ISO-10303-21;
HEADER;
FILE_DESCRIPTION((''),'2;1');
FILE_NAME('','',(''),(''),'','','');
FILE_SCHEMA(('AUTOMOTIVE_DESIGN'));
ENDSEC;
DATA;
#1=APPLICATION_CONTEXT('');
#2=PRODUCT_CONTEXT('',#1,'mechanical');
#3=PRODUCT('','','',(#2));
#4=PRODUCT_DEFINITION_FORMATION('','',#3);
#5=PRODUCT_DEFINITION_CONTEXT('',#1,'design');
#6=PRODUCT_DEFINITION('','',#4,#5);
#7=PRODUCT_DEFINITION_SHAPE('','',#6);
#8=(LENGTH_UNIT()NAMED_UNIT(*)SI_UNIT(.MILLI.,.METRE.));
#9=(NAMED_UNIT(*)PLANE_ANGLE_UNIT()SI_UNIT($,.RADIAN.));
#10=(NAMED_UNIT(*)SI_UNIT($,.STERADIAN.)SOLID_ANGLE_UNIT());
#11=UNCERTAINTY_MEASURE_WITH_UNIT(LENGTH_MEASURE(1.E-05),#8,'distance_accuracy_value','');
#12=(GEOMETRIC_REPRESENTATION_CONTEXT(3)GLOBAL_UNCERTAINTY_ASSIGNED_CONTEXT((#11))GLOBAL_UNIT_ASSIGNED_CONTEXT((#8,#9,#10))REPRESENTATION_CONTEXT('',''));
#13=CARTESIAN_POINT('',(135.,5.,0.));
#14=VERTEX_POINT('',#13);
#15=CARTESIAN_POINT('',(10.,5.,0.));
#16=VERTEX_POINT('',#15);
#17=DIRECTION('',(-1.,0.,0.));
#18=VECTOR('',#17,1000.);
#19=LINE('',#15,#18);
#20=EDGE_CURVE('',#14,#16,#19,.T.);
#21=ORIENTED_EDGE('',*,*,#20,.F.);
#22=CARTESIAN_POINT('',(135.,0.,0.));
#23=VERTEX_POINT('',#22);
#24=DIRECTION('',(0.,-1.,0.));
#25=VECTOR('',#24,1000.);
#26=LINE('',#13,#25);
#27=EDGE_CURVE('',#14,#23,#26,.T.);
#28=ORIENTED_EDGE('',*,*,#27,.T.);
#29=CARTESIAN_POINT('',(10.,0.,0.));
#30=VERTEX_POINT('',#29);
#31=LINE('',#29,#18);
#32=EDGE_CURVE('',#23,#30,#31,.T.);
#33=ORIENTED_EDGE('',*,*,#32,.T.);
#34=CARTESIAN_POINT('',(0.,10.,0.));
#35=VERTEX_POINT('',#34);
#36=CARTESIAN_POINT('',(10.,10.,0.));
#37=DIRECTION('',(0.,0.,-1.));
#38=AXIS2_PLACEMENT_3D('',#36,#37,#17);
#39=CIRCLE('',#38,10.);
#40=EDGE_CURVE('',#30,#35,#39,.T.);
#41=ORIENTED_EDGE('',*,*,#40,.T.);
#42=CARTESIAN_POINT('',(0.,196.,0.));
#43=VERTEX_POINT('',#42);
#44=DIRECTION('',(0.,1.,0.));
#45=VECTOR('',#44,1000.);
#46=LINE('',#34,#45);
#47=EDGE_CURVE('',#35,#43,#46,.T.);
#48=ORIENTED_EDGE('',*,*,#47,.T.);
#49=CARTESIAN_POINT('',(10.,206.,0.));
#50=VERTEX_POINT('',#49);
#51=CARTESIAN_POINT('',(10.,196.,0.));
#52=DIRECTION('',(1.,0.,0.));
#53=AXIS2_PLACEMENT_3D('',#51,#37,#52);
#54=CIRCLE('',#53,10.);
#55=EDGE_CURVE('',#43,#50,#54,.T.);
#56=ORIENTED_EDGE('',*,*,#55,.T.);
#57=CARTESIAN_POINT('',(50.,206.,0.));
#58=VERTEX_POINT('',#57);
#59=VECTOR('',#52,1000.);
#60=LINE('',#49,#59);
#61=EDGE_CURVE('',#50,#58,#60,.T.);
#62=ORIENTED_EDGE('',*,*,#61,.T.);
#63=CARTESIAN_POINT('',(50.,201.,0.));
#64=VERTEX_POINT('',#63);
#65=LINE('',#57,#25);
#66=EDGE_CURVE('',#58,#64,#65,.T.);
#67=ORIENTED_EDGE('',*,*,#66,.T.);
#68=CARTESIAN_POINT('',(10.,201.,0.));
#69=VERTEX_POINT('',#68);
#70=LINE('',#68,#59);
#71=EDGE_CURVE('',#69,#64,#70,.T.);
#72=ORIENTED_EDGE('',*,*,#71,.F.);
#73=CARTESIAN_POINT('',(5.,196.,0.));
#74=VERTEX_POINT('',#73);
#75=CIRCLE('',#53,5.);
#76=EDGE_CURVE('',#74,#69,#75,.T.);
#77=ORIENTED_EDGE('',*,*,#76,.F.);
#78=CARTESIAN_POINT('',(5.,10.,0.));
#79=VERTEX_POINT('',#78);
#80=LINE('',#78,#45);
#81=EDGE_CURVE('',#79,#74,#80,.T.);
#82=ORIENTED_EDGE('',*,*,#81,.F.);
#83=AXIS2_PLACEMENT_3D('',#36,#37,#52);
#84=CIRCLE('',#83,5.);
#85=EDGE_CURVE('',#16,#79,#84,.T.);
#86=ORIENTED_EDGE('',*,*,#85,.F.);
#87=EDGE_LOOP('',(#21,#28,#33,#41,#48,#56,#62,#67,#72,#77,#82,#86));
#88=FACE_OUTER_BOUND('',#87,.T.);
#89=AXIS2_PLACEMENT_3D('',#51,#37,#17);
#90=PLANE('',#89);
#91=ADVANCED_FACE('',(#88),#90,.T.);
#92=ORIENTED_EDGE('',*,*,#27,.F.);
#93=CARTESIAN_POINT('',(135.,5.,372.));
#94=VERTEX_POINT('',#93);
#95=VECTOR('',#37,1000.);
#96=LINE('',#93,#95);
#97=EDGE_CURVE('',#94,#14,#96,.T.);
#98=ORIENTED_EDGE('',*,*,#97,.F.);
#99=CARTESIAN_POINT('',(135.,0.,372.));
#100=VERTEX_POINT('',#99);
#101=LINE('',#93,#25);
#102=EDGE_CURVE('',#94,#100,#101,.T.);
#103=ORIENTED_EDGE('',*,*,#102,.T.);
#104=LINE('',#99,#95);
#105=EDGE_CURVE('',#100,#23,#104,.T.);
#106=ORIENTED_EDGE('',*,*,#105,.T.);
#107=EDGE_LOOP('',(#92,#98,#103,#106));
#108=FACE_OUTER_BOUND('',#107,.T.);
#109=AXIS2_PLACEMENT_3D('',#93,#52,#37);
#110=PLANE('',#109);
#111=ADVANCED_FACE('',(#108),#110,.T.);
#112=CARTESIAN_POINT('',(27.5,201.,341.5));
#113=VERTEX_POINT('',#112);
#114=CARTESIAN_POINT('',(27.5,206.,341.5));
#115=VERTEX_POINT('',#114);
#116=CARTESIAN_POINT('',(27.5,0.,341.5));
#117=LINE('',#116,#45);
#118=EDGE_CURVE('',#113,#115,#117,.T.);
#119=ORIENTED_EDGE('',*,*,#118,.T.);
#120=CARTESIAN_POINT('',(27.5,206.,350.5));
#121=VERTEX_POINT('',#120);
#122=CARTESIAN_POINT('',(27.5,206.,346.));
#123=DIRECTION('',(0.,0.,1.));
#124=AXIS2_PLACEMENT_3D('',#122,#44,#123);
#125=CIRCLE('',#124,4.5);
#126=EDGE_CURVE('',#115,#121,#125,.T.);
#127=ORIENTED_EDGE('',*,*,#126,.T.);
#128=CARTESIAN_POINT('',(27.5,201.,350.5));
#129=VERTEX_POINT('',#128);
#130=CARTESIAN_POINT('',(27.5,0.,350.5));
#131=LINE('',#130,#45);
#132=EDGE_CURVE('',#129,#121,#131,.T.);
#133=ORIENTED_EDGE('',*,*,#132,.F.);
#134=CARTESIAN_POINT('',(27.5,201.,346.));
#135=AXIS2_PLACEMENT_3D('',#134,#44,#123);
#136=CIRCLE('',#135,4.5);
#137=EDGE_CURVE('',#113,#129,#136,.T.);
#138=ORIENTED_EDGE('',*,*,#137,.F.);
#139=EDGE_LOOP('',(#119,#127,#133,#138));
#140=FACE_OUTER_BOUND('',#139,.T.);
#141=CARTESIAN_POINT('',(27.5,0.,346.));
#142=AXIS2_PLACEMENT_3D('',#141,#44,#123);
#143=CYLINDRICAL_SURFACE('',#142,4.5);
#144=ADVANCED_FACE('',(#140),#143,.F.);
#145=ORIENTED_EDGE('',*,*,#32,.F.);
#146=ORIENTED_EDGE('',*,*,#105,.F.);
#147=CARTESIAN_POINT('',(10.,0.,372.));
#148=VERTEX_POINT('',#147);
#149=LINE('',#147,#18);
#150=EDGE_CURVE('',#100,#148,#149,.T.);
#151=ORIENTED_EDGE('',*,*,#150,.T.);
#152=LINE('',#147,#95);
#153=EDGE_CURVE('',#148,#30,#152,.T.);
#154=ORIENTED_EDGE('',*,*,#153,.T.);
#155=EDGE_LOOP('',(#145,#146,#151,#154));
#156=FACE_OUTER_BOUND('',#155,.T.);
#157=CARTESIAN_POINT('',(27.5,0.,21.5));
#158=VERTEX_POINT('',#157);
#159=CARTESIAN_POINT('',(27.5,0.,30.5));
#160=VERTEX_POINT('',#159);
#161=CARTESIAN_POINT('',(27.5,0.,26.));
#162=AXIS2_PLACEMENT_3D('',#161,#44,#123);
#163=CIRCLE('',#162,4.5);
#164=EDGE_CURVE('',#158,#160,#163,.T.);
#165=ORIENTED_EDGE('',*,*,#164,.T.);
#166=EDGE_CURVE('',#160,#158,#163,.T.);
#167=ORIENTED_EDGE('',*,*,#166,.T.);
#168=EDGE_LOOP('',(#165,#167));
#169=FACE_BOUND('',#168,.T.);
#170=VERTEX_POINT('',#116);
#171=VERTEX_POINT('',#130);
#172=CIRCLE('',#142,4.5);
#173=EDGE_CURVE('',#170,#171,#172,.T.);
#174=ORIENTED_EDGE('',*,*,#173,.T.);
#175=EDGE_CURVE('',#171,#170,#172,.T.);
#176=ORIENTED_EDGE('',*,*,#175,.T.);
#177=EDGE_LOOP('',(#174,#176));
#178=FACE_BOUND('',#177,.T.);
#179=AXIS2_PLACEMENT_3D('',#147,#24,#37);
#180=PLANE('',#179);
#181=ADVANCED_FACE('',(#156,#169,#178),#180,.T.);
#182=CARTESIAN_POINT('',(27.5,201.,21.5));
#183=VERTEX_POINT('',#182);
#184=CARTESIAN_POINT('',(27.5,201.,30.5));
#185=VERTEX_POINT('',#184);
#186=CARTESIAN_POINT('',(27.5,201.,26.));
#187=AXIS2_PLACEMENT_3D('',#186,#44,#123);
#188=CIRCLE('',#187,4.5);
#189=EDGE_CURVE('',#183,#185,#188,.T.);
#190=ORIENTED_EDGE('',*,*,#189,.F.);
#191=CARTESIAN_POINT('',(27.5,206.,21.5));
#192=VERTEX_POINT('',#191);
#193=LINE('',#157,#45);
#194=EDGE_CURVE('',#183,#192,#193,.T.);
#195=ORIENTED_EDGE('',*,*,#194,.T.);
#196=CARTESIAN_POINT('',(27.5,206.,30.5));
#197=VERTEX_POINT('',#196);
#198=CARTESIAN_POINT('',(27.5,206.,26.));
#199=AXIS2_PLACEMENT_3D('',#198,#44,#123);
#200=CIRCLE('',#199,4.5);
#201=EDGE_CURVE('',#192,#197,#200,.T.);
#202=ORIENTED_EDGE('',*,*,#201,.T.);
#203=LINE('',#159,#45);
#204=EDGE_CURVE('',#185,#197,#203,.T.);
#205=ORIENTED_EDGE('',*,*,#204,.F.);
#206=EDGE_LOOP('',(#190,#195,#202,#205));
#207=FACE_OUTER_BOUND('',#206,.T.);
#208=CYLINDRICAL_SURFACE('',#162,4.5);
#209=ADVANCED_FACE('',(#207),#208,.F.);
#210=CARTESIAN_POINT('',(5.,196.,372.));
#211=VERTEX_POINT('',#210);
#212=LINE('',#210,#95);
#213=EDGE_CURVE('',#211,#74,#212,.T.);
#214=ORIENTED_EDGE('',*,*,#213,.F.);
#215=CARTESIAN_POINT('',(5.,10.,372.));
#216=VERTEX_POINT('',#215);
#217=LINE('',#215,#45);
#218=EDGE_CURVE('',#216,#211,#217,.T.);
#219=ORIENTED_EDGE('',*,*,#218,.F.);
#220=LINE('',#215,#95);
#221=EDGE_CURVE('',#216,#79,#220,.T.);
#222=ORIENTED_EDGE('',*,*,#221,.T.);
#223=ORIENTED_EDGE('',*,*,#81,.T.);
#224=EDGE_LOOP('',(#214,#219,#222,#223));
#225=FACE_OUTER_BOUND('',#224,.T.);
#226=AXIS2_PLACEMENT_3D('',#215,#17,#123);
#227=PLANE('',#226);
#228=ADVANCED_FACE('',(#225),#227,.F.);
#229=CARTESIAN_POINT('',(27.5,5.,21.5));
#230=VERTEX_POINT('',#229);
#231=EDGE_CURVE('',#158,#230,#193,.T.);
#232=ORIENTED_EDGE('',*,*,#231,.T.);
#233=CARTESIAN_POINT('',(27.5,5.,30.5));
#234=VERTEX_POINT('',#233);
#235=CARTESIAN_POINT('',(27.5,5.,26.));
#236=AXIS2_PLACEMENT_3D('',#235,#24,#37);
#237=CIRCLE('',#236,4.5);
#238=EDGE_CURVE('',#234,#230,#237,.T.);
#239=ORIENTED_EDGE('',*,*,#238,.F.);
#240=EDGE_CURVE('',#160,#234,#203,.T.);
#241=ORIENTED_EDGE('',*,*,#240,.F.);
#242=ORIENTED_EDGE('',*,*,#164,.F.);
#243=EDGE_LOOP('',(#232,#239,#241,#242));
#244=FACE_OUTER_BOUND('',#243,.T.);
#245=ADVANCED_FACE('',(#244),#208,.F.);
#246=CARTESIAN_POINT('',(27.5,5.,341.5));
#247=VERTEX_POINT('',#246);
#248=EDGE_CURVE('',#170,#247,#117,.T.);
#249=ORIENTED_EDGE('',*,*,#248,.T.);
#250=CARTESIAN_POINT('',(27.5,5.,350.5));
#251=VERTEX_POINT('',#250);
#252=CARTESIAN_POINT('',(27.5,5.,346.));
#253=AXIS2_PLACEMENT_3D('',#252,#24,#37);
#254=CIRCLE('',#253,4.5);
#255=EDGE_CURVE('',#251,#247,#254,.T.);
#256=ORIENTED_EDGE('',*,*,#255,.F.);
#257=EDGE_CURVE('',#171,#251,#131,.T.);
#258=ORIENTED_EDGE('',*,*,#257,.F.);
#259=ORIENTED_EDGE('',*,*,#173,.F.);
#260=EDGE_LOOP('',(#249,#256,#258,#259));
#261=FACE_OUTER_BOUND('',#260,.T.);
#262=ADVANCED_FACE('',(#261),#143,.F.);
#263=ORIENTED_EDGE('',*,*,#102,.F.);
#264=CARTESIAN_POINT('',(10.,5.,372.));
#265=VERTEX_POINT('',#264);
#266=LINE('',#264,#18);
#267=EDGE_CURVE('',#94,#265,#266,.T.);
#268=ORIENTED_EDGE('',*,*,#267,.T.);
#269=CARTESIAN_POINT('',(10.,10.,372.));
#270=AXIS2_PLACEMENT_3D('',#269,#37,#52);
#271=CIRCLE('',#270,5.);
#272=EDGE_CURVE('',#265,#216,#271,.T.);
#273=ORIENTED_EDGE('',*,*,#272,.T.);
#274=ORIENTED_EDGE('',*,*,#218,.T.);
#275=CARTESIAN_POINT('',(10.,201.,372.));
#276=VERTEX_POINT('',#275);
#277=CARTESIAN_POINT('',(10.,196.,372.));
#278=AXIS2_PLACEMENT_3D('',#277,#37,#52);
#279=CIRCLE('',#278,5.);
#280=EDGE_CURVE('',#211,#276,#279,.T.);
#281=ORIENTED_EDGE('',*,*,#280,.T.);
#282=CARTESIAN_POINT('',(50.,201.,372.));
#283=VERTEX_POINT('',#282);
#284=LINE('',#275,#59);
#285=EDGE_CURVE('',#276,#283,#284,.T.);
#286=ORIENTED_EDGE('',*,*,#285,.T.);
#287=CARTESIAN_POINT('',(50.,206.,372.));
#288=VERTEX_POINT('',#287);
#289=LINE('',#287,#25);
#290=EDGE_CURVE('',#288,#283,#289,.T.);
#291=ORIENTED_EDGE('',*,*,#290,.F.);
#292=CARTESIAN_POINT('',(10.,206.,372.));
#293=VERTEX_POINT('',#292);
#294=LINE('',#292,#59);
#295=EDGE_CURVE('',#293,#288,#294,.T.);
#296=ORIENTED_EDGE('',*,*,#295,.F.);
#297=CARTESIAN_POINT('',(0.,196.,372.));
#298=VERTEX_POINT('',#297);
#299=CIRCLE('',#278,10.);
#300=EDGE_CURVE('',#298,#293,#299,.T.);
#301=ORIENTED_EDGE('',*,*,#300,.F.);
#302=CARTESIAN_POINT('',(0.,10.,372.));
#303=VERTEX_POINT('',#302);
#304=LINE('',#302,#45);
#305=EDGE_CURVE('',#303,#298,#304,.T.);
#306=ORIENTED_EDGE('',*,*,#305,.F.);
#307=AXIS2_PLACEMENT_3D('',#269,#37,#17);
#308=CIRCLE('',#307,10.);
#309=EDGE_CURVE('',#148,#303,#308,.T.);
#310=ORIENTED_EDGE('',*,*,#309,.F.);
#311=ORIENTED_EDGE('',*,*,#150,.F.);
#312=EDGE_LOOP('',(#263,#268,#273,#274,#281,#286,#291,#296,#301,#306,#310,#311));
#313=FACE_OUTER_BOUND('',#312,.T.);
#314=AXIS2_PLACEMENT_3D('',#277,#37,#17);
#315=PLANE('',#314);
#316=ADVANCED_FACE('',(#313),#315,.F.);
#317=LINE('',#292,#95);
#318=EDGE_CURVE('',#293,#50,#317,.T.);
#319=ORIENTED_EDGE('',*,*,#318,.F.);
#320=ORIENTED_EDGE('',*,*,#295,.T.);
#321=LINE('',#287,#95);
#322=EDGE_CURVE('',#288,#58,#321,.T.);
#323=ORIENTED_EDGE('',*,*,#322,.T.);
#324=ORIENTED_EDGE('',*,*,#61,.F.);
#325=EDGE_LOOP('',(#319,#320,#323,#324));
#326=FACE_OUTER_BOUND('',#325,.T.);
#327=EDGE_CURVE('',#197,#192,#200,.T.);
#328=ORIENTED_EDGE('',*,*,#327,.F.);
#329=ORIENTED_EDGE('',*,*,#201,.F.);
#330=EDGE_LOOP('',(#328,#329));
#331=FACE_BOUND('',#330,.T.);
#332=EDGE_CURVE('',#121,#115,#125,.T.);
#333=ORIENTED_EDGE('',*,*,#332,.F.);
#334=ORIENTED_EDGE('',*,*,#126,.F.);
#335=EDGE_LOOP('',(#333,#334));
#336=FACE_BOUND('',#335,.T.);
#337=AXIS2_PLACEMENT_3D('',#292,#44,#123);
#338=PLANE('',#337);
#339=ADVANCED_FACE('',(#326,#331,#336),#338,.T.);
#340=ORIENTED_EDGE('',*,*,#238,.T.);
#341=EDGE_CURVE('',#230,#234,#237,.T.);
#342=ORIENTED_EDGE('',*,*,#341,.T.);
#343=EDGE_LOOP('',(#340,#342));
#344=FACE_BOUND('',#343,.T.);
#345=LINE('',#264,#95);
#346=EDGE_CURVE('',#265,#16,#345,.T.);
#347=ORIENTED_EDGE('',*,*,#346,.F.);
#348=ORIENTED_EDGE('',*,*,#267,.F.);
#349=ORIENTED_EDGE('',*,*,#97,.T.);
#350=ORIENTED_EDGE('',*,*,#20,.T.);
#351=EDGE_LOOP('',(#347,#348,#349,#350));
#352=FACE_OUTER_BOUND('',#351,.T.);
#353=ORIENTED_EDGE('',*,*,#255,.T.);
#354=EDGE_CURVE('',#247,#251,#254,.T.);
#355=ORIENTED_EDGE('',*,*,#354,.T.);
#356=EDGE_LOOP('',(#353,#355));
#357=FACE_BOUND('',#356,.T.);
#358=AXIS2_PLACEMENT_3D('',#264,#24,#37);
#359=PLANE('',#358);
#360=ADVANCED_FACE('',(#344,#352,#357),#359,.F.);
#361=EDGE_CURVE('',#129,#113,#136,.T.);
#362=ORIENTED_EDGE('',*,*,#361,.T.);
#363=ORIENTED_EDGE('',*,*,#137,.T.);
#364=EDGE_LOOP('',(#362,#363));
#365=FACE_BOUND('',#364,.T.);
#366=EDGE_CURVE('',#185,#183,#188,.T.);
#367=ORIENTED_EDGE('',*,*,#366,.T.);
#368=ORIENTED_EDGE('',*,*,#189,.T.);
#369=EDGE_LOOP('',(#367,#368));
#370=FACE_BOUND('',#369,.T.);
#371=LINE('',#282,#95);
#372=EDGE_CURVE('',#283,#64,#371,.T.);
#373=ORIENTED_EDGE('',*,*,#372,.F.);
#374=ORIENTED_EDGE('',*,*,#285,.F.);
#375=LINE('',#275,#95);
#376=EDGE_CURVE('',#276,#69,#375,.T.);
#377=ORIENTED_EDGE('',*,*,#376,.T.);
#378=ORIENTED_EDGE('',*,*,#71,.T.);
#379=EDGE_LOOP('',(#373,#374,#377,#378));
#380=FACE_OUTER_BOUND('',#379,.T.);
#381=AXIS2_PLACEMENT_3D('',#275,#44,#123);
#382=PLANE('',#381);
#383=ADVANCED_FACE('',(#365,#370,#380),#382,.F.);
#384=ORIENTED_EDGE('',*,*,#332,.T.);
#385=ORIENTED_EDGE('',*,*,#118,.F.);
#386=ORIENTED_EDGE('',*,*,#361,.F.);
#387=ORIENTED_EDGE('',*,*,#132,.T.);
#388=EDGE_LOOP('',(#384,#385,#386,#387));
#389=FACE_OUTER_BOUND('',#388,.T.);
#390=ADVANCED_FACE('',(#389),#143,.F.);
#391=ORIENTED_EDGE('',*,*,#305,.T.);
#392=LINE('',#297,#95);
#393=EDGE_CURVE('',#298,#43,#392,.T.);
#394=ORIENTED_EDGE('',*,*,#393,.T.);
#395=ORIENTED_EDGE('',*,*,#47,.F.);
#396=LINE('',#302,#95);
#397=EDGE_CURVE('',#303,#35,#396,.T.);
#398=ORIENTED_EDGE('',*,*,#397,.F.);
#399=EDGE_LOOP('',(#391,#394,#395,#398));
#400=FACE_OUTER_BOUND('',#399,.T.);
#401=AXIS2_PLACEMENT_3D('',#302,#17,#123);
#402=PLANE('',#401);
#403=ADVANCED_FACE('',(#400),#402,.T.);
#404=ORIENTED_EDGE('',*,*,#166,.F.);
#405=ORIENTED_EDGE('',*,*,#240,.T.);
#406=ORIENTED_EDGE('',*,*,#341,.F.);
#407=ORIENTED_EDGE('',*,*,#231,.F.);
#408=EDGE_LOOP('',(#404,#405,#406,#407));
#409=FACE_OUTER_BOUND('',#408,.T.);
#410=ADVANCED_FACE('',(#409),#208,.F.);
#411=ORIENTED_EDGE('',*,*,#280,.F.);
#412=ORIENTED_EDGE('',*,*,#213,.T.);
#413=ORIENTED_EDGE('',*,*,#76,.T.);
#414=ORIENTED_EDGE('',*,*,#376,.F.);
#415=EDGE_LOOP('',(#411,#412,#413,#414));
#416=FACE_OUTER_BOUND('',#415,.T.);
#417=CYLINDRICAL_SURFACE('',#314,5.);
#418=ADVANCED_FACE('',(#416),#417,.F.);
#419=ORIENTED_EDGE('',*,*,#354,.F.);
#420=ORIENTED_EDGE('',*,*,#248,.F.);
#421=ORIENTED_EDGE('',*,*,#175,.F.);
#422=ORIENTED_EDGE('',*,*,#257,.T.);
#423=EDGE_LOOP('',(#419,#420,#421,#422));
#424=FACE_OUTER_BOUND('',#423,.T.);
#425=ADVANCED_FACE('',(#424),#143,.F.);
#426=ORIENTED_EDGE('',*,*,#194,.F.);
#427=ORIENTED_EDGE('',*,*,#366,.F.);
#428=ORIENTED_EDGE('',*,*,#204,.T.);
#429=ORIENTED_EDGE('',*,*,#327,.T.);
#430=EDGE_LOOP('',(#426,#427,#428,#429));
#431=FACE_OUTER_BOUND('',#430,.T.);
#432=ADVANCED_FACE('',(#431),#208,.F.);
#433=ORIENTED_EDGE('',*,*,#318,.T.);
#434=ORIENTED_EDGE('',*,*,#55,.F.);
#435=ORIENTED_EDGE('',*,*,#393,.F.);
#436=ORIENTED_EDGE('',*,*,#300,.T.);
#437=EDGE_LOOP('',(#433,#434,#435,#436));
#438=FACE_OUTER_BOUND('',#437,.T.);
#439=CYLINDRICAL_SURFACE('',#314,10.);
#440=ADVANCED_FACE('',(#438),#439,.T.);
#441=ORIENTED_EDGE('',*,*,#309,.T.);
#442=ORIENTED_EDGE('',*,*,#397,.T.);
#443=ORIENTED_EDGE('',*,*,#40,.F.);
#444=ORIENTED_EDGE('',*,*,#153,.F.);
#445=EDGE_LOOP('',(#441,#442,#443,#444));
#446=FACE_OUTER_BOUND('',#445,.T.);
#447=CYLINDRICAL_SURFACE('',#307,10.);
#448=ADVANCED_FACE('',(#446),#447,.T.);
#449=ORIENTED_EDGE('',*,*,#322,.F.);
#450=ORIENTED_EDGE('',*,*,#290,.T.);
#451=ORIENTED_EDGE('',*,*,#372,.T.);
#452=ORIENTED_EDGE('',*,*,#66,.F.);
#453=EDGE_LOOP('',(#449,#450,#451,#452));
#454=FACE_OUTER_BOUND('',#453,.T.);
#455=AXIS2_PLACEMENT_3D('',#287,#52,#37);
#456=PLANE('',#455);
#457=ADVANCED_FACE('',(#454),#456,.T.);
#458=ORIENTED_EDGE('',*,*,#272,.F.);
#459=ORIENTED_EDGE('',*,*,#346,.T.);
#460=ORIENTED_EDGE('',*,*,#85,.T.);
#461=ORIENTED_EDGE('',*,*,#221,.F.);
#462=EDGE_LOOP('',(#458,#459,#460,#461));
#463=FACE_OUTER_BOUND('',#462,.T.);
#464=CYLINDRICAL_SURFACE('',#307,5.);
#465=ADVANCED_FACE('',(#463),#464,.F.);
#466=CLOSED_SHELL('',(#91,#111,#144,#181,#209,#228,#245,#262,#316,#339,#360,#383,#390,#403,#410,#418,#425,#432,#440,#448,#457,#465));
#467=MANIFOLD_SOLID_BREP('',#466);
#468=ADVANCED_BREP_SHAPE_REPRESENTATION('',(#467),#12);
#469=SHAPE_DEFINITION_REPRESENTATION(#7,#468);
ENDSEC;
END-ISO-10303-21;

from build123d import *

# Parameters (mm, degrees)
EXTRUDE_THIN1_DEPTH = 372
SKETCH2_R           = 4.5
CUT_EXTRUDE1_DEPTH  = 447.144595395
LPATTERN1_COUNT     = 2
LPATTERN1_PITCH     = 320


with BuildPart() as part:
    # Sketch1 → Extrude-Thin1 (new body)
    with BuildSketch(Plane.XY):
        with BuildLine():
            Line((50, 206), (10, 206))
            ThreePointArc((10, 206), (2.928932188, 203.071067812), (0, 196))
            Line((0, 196), (0, 10))
            ThreePointArc((0, 10), (2.928932188, 2.928932188), (10, 0))
            Line((10, 0), (135, 0))
            Line((135, 0), (135, 5))
            Line((135, 5), (10, 5))
            ThreePointArc((10, 5), (6.464466094, 6.464466094), (5, 10))
            Line((5, 10), (5, 196))
            ThreePointArc((5, 196), (6.464466094, 199.535533906), (10, 201))
            Line((10, 201), (50, 201))
            Line((50, 201), (50, 206))
        make_face()
    extrude(amount=EXTRUDE_THIN1_DEPTH)

    # Sketch2 → Cut-Extrude1 (cut, through all)
    with BuildSketch(Plane(origin=(0, 206, 0), x_dir=(1, 0, 0), z_dir=(0, 1, 0))):
        with Locations(Location((27.5, -346, 0), (0, 0, 270))):
            Circle(SKETCH2_R)
    cut_extrude1 = extrude(amount=-CUT_EXTRUDE1_DEPTH, mode=Mode.SUBTRACT)

    # LPattern1: Cut-Extrude1 ×2
    with Locations(*[(0, 0, -i * LPATTERN1_PITCH) for i in range(1, LPATTERN1_COUNT)]):
        add(cut_extrude1, mode=Mode.SUBTRACT)


solid = part.part
